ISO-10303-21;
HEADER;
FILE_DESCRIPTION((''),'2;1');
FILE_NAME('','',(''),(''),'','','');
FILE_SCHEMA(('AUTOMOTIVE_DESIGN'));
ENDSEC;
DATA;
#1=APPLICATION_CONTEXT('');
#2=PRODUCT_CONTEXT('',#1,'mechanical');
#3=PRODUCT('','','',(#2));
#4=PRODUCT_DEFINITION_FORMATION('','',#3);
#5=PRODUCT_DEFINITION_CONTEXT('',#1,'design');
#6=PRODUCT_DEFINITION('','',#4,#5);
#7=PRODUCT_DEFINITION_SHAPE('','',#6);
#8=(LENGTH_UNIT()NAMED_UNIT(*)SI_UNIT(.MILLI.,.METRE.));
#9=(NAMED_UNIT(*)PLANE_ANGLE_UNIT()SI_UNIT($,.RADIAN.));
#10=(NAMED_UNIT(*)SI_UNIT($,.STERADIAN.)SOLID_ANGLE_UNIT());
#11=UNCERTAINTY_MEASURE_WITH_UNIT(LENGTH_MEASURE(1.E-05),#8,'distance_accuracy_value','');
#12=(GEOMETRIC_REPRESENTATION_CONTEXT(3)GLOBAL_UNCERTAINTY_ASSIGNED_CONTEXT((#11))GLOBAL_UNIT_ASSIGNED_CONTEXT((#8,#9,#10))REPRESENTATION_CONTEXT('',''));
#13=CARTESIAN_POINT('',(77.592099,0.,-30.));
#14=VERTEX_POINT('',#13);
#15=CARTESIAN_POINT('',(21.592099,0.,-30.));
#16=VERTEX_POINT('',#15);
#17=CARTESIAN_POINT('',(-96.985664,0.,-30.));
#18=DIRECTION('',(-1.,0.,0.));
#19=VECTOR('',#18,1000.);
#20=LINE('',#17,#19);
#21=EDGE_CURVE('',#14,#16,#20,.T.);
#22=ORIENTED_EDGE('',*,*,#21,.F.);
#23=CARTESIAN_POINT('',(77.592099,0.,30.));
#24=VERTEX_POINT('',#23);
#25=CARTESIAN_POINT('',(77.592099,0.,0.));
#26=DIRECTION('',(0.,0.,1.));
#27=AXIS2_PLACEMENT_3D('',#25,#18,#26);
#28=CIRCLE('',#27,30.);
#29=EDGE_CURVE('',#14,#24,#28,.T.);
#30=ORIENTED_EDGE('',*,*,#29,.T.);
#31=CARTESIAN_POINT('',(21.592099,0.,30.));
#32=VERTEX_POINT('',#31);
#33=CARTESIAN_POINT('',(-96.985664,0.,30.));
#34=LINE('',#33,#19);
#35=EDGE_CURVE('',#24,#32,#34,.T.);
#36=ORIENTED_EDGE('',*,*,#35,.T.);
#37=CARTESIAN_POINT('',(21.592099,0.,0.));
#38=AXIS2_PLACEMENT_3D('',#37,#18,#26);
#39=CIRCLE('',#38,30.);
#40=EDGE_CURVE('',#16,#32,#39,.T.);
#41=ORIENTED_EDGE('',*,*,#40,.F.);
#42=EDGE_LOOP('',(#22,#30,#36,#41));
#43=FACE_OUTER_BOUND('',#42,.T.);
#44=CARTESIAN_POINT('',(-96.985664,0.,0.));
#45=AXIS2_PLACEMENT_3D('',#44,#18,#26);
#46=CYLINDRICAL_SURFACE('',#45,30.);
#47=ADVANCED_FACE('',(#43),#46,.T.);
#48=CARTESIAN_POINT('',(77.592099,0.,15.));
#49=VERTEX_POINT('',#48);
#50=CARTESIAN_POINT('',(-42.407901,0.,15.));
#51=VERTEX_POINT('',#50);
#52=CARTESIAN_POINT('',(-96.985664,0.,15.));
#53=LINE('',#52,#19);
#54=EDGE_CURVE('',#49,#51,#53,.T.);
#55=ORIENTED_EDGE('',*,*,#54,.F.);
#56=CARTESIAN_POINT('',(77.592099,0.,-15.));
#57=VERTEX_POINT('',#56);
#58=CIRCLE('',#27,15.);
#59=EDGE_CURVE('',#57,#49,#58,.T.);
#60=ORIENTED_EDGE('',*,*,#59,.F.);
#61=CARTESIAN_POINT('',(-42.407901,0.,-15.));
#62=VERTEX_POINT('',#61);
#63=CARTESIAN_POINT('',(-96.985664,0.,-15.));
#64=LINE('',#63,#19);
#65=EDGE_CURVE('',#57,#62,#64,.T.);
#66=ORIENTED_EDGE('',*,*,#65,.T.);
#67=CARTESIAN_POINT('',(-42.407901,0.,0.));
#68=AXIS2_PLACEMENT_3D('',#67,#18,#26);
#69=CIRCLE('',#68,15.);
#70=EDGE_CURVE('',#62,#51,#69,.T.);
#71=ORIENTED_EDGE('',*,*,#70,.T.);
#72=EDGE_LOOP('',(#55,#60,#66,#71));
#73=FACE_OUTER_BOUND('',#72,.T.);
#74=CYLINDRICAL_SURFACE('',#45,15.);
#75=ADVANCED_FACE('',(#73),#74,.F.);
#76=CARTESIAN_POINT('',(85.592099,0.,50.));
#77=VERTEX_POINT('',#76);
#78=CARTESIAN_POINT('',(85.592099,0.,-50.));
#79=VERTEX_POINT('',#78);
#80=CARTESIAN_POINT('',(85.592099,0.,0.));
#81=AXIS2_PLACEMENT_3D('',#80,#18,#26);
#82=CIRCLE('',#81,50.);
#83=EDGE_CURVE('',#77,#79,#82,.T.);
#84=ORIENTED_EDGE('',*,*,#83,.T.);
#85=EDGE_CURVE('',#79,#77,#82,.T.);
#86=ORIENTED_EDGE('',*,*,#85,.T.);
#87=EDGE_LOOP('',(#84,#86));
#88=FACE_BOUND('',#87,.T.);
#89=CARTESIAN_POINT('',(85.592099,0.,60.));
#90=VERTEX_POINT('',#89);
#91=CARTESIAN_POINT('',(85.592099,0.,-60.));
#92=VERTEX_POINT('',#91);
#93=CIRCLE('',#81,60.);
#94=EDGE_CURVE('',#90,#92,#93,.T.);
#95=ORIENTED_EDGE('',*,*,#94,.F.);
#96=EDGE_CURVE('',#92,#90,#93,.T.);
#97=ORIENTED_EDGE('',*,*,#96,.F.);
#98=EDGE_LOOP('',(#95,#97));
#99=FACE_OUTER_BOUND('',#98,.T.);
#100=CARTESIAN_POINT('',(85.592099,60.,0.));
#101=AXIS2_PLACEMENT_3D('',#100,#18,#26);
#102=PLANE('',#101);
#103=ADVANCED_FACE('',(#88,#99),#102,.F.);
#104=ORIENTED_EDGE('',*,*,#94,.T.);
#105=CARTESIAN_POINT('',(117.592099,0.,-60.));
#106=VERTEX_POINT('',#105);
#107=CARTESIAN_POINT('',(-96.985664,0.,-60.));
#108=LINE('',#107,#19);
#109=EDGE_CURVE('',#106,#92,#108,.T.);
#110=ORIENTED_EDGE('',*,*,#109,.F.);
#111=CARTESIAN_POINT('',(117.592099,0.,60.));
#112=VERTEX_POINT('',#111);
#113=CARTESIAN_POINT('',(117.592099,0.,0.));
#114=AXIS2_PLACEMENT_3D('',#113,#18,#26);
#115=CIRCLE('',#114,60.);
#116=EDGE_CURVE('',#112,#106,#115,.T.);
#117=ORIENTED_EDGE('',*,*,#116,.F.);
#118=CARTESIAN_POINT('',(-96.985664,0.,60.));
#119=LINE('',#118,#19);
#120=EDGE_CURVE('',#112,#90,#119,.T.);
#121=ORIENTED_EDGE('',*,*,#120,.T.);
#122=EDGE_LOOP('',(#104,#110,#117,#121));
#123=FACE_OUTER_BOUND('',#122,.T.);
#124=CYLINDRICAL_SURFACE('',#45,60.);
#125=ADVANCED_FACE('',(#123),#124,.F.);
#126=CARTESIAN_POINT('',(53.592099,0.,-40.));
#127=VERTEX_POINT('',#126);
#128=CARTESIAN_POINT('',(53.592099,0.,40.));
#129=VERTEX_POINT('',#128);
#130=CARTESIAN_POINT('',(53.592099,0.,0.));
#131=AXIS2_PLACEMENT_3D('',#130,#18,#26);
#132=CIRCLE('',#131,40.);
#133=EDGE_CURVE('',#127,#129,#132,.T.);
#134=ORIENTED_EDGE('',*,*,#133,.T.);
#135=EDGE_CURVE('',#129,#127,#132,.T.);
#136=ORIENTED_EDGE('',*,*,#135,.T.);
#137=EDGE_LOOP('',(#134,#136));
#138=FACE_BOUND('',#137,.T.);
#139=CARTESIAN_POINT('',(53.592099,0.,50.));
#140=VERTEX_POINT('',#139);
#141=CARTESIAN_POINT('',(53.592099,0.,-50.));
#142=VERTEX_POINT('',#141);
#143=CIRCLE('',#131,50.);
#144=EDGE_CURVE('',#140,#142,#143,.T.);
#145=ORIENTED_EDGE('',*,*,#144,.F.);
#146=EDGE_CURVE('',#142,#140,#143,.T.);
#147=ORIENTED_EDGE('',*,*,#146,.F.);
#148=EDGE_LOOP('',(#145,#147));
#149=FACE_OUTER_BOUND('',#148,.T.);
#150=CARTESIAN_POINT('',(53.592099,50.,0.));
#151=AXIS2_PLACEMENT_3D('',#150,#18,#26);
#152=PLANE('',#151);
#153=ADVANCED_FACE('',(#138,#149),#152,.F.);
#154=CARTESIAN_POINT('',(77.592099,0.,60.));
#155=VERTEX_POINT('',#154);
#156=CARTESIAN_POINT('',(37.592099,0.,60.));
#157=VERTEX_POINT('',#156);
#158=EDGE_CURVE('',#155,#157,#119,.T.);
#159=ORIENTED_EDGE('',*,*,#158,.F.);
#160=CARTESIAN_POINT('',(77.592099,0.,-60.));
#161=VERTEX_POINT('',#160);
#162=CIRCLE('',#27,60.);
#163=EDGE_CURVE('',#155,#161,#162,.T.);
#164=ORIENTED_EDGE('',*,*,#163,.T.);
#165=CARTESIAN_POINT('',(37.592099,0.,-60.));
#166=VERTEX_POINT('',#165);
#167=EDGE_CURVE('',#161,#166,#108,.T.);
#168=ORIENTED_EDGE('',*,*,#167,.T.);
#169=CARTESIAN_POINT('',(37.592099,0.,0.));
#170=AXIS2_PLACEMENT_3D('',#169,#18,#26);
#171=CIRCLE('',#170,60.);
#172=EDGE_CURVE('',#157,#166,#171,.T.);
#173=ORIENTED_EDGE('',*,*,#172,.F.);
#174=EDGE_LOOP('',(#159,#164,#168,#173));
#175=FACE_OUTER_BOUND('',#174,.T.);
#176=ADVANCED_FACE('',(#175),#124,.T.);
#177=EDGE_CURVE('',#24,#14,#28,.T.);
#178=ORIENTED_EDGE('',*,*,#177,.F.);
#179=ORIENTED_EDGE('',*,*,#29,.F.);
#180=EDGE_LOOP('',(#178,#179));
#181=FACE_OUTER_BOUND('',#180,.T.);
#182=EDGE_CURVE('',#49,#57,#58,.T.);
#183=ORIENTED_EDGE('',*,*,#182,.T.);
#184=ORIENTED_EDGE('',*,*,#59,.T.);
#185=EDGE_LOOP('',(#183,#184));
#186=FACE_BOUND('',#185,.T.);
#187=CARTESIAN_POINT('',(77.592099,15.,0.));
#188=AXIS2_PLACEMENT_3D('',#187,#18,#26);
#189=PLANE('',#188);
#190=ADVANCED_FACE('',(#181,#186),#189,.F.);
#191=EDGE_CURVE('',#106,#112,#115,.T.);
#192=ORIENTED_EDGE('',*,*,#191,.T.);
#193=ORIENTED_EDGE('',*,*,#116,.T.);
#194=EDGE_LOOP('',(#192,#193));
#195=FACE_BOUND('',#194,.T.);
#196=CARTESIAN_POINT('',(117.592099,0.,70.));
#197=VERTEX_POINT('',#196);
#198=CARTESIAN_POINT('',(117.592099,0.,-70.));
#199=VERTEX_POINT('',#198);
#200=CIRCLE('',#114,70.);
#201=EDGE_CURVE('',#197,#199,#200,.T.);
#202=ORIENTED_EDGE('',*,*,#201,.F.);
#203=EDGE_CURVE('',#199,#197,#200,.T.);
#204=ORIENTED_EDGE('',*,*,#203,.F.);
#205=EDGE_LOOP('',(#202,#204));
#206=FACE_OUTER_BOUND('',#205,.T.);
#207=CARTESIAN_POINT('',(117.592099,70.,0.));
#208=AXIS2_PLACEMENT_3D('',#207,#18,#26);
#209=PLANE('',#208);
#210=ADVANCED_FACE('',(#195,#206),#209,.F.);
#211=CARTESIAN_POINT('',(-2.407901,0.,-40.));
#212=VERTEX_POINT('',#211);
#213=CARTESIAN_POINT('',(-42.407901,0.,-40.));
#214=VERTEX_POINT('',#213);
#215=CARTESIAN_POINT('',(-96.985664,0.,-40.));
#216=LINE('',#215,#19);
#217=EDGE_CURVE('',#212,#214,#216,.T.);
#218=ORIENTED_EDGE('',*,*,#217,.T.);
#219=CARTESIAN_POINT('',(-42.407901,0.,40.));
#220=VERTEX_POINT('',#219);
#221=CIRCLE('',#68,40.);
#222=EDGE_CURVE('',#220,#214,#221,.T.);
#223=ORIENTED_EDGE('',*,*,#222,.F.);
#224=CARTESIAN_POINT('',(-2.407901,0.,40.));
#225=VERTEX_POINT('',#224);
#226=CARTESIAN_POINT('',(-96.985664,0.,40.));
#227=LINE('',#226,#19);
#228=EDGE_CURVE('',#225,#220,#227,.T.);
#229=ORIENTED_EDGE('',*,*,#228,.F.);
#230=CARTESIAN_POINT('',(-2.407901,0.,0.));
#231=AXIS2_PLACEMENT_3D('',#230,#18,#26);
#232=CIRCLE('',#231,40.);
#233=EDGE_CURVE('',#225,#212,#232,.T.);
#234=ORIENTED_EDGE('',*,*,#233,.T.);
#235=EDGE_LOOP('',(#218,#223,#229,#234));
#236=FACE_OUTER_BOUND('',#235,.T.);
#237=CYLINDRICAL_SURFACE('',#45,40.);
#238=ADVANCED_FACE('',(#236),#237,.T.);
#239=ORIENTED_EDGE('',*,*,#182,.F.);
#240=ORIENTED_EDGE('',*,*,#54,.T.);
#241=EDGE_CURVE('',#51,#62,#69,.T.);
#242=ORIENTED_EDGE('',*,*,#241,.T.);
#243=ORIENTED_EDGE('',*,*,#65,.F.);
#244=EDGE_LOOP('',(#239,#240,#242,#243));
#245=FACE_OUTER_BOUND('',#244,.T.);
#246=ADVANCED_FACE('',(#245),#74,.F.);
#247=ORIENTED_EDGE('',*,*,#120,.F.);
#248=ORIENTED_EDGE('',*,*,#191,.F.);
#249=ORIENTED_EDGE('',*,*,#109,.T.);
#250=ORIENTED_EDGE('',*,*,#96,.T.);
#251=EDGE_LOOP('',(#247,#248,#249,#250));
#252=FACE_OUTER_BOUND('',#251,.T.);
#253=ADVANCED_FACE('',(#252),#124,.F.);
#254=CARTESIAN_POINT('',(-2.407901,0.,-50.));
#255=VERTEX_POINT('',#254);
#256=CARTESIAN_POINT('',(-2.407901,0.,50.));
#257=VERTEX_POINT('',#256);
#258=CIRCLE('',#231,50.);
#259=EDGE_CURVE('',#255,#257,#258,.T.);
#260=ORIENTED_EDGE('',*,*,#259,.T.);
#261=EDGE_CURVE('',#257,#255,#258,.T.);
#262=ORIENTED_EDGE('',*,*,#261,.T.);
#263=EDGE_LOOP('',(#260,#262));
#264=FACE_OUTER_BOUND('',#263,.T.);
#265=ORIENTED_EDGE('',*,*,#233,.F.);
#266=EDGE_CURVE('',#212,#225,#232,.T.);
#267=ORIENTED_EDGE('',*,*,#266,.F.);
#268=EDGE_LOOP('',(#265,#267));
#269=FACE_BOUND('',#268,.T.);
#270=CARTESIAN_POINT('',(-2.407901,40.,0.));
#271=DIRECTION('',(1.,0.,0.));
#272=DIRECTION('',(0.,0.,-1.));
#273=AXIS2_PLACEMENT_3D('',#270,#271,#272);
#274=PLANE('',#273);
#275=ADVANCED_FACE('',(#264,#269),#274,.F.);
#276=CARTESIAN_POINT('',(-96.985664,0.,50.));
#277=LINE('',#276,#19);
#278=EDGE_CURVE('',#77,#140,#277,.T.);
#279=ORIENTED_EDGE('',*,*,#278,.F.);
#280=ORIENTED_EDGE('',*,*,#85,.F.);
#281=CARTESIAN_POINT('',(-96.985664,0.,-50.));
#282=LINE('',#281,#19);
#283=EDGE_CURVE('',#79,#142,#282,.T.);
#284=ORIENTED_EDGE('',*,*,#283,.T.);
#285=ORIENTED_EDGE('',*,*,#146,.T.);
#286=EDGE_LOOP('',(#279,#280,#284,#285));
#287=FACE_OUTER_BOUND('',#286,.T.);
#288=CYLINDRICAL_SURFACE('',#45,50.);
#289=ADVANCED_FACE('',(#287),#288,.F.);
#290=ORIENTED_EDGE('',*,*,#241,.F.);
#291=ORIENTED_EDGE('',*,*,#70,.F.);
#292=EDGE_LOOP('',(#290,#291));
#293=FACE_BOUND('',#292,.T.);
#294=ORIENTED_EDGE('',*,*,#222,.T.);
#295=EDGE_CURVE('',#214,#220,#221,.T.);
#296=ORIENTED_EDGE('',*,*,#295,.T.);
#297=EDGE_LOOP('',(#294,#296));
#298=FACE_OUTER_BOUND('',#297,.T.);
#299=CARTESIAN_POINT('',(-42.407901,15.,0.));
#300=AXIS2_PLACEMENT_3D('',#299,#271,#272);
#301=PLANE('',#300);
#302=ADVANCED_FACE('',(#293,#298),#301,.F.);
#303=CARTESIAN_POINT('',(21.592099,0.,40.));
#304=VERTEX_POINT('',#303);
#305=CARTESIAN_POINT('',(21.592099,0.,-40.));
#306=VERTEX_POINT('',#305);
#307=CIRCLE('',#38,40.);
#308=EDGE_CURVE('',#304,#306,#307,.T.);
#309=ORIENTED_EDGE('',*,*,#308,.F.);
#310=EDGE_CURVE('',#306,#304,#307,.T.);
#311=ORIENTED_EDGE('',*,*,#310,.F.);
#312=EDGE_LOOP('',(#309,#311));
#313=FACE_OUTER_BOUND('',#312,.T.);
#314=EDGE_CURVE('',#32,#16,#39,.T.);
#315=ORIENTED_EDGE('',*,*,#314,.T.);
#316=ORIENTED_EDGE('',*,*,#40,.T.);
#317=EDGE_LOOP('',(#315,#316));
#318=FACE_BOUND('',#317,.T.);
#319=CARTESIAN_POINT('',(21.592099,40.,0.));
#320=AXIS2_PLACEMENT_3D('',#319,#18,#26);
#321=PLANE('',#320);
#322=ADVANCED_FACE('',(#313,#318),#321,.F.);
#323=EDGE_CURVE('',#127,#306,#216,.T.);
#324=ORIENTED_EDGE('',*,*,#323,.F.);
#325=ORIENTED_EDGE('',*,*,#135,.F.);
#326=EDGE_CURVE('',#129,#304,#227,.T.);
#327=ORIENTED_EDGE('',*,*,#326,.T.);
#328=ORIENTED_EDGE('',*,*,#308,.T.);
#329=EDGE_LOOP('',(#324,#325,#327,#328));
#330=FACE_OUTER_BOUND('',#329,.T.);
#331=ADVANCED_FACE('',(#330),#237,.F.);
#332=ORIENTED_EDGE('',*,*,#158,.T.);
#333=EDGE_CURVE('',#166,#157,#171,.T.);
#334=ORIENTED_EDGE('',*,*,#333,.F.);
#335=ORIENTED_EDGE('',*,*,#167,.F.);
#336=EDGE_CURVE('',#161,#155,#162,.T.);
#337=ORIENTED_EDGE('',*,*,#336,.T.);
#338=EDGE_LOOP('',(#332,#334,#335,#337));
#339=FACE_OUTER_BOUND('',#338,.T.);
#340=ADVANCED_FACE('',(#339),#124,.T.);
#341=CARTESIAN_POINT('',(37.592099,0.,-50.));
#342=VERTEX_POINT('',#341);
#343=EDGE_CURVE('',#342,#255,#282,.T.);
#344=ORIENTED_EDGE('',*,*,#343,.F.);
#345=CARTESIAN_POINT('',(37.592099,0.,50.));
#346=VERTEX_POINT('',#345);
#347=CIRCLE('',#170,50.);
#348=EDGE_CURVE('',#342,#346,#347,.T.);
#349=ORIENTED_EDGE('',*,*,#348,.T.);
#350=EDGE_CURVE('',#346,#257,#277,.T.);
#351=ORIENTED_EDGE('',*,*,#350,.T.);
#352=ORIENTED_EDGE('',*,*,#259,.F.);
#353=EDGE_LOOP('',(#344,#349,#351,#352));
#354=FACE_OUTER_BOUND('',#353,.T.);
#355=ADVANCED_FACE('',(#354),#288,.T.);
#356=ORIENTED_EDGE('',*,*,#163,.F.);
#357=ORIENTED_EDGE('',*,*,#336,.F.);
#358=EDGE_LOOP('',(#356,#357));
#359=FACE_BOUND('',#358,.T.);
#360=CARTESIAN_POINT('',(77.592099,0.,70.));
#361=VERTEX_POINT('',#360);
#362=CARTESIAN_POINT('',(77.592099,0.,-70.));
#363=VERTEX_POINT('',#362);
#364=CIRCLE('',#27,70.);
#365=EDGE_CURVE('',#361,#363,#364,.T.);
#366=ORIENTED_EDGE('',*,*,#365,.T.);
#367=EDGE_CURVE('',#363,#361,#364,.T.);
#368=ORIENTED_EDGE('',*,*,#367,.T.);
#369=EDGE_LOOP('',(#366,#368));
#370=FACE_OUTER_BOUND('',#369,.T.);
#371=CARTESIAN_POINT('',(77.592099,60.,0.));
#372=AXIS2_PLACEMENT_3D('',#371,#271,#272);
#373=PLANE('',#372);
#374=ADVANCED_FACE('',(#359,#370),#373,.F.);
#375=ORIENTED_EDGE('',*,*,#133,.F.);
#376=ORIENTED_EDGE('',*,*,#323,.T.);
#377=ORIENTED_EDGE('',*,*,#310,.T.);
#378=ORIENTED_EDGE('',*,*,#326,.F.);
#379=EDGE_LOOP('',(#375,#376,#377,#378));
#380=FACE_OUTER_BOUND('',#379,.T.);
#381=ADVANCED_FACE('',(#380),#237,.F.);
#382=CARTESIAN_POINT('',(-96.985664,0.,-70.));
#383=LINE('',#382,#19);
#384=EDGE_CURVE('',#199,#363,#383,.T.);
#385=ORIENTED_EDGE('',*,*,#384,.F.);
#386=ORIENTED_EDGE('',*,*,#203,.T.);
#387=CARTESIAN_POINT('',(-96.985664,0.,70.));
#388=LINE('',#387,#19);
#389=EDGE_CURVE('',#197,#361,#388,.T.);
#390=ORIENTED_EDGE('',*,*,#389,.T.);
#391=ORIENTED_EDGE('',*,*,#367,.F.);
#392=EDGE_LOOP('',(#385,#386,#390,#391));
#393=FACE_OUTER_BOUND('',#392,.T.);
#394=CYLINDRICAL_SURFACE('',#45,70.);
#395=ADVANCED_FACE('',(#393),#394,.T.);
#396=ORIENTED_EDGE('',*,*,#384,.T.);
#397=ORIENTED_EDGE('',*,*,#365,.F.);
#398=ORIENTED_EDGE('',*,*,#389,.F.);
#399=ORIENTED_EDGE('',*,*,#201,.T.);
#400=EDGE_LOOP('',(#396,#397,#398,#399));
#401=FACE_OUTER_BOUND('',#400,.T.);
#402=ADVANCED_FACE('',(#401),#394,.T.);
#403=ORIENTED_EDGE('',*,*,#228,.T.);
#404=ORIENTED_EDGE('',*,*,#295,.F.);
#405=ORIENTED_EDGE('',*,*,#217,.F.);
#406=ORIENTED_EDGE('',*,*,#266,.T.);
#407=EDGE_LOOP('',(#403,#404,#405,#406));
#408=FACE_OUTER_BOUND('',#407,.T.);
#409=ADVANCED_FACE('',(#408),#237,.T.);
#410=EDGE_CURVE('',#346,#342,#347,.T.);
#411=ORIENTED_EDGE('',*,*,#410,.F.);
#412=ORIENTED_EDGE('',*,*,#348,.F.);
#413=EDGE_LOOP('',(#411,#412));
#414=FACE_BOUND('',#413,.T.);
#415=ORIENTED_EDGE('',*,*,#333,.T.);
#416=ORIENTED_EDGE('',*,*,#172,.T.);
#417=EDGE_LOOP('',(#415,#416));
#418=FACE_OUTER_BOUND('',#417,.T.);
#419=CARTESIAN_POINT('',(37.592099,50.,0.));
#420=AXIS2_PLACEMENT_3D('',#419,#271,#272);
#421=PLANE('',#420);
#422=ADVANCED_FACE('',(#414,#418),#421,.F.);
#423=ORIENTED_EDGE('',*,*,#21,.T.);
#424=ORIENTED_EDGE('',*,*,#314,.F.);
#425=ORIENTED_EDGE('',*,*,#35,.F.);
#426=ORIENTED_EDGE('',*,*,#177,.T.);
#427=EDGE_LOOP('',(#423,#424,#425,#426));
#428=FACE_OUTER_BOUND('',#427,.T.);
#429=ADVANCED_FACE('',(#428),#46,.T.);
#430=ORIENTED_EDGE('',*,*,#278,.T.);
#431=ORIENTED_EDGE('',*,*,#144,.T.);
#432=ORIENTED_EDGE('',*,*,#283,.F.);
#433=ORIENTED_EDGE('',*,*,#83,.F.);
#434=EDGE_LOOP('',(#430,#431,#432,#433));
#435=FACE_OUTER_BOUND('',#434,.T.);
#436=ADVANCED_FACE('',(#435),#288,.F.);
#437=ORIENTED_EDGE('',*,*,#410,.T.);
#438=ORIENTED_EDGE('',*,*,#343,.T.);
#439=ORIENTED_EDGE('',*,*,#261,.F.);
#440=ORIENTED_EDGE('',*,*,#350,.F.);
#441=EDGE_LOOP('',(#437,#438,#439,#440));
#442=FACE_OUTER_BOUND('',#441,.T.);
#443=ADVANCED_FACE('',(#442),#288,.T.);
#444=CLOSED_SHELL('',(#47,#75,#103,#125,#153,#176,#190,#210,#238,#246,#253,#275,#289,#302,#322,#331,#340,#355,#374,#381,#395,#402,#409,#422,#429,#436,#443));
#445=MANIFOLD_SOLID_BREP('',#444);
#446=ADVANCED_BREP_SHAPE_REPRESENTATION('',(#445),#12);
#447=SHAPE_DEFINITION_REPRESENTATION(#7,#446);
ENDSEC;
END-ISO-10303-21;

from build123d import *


with BuildPart() as part:
    # Stepped Bushing Profile → Stepped Bushing Revolve (revolve)
    with BuildSketch(Plane.XY, mode=Mode.PRIVATE) as stepped_bushing_revolve_sk:
        Polygon((-42.407900521, 15), (-42.407900521, 40), (-2.407900521, 40), (-2.407900521, 50), (37.592099479, 50), (37.592099479, 60), (77.592099479, 60), (77.592099479, 70), (117.592099479, 70), (117.592099479, 60), (85.592099479, 60), (85.592099479, 50), (53.592099479, 50), (53.592099479, 40), (21.592099479, 40), (21.592099479, 30), (77.592099479, 30), (77.592099479, 15), align=None)
    revolve(stepped_bushing_revolve_sk.sketch.rotate(Axis((-96.985663619, 0, 0), (1, 0, 0)), 90), axis=Axis((-96.985663619, 0, 0), (1, 0, 0)))


solid = part.part
